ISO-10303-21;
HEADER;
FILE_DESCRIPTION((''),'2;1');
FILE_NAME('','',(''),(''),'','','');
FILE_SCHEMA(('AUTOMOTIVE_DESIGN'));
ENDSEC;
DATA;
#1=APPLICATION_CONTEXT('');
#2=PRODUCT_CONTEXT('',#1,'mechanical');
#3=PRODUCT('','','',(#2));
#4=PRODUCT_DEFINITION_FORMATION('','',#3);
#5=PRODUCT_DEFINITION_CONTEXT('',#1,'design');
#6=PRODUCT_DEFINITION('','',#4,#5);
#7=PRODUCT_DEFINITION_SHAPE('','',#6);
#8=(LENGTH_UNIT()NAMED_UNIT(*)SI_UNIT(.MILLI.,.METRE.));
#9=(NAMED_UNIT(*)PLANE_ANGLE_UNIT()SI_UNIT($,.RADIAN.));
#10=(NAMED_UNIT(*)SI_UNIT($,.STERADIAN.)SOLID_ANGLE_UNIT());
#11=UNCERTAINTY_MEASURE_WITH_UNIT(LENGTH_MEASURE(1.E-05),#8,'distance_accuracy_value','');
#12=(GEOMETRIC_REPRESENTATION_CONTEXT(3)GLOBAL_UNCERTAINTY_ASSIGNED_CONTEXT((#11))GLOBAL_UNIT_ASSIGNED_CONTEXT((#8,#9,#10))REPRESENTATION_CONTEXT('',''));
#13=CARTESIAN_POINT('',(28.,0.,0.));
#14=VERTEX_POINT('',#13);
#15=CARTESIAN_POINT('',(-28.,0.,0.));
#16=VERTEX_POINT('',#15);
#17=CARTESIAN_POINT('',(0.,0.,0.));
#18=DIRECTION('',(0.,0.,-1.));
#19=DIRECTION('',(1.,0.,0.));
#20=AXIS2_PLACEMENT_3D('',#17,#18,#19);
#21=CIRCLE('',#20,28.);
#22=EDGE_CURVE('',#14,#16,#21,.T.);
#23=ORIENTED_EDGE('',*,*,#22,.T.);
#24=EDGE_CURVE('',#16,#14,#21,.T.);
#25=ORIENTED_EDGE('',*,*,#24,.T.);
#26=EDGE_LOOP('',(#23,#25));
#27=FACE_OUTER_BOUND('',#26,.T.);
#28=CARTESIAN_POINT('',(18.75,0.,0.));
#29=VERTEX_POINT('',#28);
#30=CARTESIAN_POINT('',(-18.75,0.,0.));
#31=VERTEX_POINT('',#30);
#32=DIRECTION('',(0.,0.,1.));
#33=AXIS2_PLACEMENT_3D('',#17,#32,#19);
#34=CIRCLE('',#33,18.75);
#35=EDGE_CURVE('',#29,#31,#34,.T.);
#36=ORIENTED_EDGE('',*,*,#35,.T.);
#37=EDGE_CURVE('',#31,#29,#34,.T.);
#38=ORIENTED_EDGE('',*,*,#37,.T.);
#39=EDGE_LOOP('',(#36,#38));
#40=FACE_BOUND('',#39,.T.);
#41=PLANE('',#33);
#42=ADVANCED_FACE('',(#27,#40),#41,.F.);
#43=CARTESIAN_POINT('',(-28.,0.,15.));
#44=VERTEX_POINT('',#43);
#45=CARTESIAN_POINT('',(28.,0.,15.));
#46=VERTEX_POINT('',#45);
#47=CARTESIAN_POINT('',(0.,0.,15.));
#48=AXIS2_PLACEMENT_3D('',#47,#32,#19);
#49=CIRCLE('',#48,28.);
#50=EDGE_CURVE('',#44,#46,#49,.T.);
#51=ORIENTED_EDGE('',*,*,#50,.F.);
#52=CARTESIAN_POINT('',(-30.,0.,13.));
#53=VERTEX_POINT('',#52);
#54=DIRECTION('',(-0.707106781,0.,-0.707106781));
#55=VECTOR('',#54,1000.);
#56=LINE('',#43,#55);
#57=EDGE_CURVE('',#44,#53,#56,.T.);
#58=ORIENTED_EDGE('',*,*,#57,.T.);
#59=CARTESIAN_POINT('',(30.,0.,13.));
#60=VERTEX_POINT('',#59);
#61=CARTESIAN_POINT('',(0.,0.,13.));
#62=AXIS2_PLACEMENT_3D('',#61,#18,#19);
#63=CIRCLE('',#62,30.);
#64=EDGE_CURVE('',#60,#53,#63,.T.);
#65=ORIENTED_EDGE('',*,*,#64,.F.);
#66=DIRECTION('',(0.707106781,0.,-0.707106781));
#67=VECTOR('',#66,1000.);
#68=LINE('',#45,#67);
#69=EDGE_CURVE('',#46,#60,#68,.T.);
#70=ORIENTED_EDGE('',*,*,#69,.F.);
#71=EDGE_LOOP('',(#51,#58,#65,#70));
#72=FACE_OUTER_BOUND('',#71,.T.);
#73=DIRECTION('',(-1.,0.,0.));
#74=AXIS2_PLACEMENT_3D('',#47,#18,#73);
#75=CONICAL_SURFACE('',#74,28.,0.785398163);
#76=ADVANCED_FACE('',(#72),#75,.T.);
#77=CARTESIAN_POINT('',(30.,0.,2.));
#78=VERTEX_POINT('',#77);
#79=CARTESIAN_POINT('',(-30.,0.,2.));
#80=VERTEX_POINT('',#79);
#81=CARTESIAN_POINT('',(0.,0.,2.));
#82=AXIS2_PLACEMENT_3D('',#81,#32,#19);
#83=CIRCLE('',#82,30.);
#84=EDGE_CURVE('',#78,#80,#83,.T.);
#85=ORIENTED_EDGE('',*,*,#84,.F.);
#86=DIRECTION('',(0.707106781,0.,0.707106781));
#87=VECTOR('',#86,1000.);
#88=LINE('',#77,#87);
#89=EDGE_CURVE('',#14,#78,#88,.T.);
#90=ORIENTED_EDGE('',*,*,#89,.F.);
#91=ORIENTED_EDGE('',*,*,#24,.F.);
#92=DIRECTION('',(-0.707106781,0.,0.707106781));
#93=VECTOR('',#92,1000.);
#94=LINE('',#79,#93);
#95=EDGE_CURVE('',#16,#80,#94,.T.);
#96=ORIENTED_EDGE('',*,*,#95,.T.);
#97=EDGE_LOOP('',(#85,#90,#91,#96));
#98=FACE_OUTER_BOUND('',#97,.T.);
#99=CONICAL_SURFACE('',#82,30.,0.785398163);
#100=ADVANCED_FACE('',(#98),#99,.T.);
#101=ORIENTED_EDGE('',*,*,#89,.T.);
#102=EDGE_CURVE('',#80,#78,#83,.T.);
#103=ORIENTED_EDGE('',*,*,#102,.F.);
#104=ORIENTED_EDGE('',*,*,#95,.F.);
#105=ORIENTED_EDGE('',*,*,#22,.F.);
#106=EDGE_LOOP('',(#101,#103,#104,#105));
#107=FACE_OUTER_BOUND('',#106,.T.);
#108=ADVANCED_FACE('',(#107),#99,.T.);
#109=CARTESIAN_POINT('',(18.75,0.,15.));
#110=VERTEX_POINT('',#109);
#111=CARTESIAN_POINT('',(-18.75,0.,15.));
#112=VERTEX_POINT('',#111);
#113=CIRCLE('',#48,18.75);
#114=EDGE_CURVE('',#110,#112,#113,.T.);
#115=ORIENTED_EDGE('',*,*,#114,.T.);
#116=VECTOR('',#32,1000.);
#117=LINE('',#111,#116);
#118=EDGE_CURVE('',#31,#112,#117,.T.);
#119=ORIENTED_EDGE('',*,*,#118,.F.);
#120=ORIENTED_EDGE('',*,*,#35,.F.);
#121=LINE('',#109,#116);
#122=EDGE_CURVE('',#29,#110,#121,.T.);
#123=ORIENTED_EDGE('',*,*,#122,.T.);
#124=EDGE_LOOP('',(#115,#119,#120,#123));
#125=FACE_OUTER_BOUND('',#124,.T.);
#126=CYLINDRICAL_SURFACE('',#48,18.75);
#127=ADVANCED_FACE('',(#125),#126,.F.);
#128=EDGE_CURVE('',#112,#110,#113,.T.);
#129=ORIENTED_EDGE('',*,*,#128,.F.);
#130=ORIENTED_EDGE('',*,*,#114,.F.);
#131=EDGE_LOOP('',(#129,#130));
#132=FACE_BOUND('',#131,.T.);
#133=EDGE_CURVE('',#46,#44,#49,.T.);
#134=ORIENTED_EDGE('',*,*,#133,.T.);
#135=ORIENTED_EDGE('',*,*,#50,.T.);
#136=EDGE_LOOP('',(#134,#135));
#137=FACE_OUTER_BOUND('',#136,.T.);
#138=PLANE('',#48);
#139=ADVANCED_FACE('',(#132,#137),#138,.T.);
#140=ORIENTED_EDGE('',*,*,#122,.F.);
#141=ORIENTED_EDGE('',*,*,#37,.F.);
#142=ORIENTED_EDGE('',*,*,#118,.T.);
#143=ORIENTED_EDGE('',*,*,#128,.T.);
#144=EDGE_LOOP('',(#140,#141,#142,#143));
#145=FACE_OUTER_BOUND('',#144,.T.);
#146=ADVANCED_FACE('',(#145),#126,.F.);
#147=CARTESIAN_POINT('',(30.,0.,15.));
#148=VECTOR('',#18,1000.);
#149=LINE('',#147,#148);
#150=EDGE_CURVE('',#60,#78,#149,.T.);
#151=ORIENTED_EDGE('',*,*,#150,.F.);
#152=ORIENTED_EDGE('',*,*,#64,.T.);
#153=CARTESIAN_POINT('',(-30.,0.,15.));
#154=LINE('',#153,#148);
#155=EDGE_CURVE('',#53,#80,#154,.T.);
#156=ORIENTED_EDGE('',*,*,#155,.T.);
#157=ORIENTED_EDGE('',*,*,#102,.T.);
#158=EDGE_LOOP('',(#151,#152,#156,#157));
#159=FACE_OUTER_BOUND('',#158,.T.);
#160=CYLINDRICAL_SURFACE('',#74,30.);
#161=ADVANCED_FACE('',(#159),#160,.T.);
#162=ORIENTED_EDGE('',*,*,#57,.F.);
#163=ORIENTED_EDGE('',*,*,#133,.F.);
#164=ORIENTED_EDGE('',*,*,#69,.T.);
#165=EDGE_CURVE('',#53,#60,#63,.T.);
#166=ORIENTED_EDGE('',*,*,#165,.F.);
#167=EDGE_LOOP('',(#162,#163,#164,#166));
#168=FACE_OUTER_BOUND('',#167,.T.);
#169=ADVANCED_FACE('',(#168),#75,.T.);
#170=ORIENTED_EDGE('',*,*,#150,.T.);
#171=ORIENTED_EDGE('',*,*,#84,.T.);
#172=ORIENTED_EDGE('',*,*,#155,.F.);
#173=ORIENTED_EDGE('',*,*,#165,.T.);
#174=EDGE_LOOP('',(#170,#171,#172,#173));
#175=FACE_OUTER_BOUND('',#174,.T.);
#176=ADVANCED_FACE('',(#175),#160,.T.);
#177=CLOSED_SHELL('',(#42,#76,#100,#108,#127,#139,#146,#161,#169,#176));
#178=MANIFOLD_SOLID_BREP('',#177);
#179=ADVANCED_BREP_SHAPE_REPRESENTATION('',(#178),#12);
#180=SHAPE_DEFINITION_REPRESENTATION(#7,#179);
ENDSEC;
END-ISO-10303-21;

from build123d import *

# Parameters (mm, degrees)
SKETCH1_R              = 30
BOSS_EXTRUDE1_DEPTH    = 15
SKETCH2_R              = 17.5
CUT_EXTRUDE1_DEPTH     = 15
CHAMFER1_SIZE          = 2
M42_TAPPED_HOLE4_D     = 37.5
M42_TAPPED_HOLE4_DEPTH = 106.5
M42_TAPPED_HOLE4_TIP   = 11.266136607


with BuildPart() as part:
    # Sketch1 → Boss-Extrude1 (new body)
    with BuildSketch(Plane.XY):
        Circle(SKETCH1_R)
    extrude(amount=BOSS_EXTRUDE1_DEPTH)

    # Sketch2 → Cut-Extrude1 (cut)
    with BuildSketch(Plane.XY.offset(15)):
        Circle(SKETCH2_R)
    extrude(amount=-CUT_EXTRUDE1_DEPTH, mode=Mode.SUBTRACT)

    # Chamfer1
    chamfer1_edges = [part.edges().sort_by_distance(p)[0] for p in [
        (-30, 0, 0),
        (-30, 0, 15),
    ]]
    chamfer(chamfer1_edges, length=CHAMFER1_SIZE)

    # M42 Tapped Hole4
    with Locations(Plane.XY.offset(15)):
        with Locations((0, 0)):
            Hole(M42_TAPPED_HOLE4_D / 2, depth=M42_TAPPED_HOLE4_DEPTH)
            with Locations((0, 0, -(M42_TAPPED_HOLE4_DEPTH + M42_TAPPED_HOLE4_TIP / 2))):  # 118° drill point
                Cone(0, M42_TAPPED_HOLE4_D / 2, M42_TAPPED_HOLE4_TIP, mode=Mode.SUBTRACT)


solid = part.part
